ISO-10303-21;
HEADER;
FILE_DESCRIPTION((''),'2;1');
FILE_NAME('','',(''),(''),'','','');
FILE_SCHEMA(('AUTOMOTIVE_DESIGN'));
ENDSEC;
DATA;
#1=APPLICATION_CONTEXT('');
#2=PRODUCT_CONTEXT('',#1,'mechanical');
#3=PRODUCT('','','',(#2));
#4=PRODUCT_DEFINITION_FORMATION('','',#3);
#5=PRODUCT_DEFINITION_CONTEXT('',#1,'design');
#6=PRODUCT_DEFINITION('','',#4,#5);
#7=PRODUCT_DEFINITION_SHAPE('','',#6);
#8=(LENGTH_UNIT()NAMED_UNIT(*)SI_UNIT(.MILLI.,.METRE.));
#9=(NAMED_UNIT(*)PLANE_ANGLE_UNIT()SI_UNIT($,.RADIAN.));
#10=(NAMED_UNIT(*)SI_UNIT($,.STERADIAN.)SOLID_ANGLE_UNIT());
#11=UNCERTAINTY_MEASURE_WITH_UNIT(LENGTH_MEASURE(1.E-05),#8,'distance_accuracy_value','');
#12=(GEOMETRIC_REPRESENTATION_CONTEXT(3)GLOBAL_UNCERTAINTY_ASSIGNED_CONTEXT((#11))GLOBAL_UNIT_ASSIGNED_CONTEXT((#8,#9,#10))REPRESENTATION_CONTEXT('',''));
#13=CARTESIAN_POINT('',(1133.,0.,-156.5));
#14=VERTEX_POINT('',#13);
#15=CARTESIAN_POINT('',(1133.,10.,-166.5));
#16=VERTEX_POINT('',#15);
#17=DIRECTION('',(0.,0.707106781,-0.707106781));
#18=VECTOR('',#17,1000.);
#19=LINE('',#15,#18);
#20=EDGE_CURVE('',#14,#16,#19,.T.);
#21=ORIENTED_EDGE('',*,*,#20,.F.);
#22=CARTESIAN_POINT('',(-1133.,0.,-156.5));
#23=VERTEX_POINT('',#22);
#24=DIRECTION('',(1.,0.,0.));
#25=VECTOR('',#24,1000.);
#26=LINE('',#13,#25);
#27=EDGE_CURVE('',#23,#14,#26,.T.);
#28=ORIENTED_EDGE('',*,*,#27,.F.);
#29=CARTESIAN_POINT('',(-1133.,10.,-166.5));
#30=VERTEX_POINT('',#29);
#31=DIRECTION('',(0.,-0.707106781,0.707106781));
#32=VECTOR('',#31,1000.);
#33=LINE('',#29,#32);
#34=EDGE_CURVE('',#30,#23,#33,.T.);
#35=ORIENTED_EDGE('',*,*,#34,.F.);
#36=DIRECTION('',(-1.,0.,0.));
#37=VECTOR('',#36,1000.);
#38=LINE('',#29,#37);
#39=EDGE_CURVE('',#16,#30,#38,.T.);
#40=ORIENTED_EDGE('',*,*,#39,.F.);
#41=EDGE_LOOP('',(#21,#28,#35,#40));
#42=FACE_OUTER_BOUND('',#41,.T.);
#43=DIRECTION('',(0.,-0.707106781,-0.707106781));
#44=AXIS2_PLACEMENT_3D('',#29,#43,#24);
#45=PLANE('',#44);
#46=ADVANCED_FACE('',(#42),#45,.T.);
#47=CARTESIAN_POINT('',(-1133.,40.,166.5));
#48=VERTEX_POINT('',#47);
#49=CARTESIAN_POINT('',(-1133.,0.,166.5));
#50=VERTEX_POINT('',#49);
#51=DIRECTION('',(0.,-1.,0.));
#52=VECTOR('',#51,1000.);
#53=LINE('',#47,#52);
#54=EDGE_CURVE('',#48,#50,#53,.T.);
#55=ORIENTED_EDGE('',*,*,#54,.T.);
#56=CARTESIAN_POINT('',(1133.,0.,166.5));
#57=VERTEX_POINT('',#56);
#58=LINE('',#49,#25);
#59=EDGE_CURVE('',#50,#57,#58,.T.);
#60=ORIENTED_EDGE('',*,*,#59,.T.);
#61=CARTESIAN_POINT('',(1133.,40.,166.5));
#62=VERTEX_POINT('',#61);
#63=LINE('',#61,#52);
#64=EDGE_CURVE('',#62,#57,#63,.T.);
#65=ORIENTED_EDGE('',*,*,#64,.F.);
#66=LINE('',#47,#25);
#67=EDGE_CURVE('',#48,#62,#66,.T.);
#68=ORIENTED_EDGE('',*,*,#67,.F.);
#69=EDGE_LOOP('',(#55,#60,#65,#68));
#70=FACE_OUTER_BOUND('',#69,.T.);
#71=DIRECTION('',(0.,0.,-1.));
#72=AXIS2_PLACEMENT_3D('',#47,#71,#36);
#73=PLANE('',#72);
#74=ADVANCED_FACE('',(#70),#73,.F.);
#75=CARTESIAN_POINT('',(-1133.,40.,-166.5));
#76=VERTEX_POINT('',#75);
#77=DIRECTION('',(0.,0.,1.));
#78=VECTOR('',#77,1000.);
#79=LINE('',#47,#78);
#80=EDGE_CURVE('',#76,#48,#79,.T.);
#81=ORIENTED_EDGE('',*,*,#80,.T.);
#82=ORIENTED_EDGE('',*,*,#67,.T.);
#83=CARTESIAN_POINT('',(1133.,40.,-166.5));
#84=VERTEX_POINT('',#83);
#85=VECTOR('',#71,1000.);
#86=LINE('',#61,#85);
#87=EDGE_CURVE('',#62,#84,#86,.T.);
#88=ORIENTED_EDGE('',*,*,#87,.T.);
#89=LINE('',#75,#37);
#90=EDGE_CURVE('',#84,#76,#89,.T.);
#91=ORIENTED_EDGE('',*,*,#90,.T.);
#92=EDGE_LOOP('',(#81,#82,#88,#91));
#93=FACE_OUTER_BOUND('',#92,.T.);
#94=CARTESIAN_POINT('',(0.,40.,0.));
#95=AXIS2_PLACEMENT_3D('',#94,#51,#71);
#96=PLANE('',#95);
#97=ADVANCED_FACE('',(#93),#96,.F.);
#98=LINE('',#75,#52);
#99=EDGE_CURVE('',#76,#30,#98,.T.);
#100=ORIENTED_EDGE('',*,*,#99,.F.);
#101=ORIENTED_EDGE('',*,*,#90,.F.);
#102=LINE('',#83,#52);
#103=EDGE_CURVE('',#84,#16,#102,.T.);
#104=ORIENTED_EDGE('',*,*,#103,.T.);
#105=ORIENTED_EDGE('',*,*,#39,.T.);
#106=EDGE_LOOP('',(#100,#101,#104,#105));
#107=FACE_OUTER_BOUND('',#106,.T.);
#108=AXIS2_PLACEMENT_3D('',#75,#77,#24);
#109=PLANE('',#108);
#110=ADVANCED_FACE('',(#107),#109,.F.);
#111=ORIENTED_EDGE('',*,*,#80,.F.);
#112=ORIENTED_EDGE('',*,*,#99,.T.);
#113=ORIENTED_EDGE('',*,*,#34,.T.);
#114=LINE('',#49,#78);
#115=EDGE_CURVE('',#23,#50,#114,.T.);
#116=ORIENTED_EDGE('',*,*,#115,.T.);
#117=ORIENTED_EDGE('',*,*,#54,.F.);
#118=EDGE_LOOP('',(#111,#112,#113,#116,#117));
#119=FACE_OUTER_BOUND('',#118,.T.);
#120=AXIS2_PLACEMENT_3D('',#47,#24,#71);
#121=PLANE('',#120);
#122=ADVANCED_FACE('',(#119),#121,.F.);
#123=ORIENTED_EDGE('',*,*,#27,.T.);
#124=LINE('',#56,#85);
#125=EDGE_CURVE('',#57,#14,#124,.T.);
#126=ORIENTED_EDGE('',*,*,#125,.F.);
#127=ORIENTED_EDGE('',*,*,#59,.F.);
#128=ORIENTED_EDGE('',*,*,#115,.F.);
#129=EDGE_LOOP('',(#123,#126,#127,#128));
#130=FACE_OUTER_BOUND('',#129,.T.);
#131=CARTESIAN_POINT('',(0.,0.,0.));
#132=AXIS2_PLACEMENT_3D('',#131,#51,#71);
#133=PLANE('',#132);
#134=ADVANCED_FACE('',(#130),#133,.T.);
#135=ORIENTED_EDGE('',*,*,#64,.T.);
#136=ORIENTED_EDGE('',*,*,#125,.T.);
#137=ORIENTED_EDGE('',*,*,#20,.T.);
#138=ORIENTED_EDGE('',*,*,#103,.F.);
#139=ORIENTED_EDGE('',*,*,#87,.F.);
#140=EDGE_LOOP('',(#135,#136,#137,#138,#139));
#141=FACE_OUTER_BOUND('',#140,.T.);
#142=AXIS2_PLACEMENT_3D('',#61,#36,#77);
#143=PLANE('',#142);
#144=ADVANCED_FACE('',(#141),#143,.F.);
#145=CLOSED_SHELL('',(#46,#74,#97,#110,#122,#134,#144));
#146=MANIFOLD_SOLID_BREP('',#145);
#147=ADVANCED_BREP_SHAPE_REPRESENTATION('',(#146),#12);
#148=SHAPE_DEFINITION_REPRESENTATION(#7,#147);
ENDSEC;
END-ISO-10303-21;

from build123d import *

# Parameters (mm, degrees)
SKETCH_1_W      = 2266
SKETCH_1_H      = 333
EXTRUDE_1_DEPTH = 40
CHAMFER_1_SIZE  = 10


with BuildPart() as part:
    # 草图1 → 凸台-拉伸1 (new body)
    with BuildSketch(Plane(origin=(0, 0, 0), x_dir=(1, 0, 0), z_dir=(0, 1, 0))):
        Rectangle(SKETCH_1_W, SKETCH_1_H)
    extrude(amount=EXTRUDE_1_DEPTH)

    # 倒角1
    chamfer_1_edges = [part.edges().sort_by_distance(p)[0] for p in [
        (0, 0, -166.5),
    ]]
    chamfer(chamfer_1_edges, length=CHAMFER_1_SIZE)


solid = part.part
